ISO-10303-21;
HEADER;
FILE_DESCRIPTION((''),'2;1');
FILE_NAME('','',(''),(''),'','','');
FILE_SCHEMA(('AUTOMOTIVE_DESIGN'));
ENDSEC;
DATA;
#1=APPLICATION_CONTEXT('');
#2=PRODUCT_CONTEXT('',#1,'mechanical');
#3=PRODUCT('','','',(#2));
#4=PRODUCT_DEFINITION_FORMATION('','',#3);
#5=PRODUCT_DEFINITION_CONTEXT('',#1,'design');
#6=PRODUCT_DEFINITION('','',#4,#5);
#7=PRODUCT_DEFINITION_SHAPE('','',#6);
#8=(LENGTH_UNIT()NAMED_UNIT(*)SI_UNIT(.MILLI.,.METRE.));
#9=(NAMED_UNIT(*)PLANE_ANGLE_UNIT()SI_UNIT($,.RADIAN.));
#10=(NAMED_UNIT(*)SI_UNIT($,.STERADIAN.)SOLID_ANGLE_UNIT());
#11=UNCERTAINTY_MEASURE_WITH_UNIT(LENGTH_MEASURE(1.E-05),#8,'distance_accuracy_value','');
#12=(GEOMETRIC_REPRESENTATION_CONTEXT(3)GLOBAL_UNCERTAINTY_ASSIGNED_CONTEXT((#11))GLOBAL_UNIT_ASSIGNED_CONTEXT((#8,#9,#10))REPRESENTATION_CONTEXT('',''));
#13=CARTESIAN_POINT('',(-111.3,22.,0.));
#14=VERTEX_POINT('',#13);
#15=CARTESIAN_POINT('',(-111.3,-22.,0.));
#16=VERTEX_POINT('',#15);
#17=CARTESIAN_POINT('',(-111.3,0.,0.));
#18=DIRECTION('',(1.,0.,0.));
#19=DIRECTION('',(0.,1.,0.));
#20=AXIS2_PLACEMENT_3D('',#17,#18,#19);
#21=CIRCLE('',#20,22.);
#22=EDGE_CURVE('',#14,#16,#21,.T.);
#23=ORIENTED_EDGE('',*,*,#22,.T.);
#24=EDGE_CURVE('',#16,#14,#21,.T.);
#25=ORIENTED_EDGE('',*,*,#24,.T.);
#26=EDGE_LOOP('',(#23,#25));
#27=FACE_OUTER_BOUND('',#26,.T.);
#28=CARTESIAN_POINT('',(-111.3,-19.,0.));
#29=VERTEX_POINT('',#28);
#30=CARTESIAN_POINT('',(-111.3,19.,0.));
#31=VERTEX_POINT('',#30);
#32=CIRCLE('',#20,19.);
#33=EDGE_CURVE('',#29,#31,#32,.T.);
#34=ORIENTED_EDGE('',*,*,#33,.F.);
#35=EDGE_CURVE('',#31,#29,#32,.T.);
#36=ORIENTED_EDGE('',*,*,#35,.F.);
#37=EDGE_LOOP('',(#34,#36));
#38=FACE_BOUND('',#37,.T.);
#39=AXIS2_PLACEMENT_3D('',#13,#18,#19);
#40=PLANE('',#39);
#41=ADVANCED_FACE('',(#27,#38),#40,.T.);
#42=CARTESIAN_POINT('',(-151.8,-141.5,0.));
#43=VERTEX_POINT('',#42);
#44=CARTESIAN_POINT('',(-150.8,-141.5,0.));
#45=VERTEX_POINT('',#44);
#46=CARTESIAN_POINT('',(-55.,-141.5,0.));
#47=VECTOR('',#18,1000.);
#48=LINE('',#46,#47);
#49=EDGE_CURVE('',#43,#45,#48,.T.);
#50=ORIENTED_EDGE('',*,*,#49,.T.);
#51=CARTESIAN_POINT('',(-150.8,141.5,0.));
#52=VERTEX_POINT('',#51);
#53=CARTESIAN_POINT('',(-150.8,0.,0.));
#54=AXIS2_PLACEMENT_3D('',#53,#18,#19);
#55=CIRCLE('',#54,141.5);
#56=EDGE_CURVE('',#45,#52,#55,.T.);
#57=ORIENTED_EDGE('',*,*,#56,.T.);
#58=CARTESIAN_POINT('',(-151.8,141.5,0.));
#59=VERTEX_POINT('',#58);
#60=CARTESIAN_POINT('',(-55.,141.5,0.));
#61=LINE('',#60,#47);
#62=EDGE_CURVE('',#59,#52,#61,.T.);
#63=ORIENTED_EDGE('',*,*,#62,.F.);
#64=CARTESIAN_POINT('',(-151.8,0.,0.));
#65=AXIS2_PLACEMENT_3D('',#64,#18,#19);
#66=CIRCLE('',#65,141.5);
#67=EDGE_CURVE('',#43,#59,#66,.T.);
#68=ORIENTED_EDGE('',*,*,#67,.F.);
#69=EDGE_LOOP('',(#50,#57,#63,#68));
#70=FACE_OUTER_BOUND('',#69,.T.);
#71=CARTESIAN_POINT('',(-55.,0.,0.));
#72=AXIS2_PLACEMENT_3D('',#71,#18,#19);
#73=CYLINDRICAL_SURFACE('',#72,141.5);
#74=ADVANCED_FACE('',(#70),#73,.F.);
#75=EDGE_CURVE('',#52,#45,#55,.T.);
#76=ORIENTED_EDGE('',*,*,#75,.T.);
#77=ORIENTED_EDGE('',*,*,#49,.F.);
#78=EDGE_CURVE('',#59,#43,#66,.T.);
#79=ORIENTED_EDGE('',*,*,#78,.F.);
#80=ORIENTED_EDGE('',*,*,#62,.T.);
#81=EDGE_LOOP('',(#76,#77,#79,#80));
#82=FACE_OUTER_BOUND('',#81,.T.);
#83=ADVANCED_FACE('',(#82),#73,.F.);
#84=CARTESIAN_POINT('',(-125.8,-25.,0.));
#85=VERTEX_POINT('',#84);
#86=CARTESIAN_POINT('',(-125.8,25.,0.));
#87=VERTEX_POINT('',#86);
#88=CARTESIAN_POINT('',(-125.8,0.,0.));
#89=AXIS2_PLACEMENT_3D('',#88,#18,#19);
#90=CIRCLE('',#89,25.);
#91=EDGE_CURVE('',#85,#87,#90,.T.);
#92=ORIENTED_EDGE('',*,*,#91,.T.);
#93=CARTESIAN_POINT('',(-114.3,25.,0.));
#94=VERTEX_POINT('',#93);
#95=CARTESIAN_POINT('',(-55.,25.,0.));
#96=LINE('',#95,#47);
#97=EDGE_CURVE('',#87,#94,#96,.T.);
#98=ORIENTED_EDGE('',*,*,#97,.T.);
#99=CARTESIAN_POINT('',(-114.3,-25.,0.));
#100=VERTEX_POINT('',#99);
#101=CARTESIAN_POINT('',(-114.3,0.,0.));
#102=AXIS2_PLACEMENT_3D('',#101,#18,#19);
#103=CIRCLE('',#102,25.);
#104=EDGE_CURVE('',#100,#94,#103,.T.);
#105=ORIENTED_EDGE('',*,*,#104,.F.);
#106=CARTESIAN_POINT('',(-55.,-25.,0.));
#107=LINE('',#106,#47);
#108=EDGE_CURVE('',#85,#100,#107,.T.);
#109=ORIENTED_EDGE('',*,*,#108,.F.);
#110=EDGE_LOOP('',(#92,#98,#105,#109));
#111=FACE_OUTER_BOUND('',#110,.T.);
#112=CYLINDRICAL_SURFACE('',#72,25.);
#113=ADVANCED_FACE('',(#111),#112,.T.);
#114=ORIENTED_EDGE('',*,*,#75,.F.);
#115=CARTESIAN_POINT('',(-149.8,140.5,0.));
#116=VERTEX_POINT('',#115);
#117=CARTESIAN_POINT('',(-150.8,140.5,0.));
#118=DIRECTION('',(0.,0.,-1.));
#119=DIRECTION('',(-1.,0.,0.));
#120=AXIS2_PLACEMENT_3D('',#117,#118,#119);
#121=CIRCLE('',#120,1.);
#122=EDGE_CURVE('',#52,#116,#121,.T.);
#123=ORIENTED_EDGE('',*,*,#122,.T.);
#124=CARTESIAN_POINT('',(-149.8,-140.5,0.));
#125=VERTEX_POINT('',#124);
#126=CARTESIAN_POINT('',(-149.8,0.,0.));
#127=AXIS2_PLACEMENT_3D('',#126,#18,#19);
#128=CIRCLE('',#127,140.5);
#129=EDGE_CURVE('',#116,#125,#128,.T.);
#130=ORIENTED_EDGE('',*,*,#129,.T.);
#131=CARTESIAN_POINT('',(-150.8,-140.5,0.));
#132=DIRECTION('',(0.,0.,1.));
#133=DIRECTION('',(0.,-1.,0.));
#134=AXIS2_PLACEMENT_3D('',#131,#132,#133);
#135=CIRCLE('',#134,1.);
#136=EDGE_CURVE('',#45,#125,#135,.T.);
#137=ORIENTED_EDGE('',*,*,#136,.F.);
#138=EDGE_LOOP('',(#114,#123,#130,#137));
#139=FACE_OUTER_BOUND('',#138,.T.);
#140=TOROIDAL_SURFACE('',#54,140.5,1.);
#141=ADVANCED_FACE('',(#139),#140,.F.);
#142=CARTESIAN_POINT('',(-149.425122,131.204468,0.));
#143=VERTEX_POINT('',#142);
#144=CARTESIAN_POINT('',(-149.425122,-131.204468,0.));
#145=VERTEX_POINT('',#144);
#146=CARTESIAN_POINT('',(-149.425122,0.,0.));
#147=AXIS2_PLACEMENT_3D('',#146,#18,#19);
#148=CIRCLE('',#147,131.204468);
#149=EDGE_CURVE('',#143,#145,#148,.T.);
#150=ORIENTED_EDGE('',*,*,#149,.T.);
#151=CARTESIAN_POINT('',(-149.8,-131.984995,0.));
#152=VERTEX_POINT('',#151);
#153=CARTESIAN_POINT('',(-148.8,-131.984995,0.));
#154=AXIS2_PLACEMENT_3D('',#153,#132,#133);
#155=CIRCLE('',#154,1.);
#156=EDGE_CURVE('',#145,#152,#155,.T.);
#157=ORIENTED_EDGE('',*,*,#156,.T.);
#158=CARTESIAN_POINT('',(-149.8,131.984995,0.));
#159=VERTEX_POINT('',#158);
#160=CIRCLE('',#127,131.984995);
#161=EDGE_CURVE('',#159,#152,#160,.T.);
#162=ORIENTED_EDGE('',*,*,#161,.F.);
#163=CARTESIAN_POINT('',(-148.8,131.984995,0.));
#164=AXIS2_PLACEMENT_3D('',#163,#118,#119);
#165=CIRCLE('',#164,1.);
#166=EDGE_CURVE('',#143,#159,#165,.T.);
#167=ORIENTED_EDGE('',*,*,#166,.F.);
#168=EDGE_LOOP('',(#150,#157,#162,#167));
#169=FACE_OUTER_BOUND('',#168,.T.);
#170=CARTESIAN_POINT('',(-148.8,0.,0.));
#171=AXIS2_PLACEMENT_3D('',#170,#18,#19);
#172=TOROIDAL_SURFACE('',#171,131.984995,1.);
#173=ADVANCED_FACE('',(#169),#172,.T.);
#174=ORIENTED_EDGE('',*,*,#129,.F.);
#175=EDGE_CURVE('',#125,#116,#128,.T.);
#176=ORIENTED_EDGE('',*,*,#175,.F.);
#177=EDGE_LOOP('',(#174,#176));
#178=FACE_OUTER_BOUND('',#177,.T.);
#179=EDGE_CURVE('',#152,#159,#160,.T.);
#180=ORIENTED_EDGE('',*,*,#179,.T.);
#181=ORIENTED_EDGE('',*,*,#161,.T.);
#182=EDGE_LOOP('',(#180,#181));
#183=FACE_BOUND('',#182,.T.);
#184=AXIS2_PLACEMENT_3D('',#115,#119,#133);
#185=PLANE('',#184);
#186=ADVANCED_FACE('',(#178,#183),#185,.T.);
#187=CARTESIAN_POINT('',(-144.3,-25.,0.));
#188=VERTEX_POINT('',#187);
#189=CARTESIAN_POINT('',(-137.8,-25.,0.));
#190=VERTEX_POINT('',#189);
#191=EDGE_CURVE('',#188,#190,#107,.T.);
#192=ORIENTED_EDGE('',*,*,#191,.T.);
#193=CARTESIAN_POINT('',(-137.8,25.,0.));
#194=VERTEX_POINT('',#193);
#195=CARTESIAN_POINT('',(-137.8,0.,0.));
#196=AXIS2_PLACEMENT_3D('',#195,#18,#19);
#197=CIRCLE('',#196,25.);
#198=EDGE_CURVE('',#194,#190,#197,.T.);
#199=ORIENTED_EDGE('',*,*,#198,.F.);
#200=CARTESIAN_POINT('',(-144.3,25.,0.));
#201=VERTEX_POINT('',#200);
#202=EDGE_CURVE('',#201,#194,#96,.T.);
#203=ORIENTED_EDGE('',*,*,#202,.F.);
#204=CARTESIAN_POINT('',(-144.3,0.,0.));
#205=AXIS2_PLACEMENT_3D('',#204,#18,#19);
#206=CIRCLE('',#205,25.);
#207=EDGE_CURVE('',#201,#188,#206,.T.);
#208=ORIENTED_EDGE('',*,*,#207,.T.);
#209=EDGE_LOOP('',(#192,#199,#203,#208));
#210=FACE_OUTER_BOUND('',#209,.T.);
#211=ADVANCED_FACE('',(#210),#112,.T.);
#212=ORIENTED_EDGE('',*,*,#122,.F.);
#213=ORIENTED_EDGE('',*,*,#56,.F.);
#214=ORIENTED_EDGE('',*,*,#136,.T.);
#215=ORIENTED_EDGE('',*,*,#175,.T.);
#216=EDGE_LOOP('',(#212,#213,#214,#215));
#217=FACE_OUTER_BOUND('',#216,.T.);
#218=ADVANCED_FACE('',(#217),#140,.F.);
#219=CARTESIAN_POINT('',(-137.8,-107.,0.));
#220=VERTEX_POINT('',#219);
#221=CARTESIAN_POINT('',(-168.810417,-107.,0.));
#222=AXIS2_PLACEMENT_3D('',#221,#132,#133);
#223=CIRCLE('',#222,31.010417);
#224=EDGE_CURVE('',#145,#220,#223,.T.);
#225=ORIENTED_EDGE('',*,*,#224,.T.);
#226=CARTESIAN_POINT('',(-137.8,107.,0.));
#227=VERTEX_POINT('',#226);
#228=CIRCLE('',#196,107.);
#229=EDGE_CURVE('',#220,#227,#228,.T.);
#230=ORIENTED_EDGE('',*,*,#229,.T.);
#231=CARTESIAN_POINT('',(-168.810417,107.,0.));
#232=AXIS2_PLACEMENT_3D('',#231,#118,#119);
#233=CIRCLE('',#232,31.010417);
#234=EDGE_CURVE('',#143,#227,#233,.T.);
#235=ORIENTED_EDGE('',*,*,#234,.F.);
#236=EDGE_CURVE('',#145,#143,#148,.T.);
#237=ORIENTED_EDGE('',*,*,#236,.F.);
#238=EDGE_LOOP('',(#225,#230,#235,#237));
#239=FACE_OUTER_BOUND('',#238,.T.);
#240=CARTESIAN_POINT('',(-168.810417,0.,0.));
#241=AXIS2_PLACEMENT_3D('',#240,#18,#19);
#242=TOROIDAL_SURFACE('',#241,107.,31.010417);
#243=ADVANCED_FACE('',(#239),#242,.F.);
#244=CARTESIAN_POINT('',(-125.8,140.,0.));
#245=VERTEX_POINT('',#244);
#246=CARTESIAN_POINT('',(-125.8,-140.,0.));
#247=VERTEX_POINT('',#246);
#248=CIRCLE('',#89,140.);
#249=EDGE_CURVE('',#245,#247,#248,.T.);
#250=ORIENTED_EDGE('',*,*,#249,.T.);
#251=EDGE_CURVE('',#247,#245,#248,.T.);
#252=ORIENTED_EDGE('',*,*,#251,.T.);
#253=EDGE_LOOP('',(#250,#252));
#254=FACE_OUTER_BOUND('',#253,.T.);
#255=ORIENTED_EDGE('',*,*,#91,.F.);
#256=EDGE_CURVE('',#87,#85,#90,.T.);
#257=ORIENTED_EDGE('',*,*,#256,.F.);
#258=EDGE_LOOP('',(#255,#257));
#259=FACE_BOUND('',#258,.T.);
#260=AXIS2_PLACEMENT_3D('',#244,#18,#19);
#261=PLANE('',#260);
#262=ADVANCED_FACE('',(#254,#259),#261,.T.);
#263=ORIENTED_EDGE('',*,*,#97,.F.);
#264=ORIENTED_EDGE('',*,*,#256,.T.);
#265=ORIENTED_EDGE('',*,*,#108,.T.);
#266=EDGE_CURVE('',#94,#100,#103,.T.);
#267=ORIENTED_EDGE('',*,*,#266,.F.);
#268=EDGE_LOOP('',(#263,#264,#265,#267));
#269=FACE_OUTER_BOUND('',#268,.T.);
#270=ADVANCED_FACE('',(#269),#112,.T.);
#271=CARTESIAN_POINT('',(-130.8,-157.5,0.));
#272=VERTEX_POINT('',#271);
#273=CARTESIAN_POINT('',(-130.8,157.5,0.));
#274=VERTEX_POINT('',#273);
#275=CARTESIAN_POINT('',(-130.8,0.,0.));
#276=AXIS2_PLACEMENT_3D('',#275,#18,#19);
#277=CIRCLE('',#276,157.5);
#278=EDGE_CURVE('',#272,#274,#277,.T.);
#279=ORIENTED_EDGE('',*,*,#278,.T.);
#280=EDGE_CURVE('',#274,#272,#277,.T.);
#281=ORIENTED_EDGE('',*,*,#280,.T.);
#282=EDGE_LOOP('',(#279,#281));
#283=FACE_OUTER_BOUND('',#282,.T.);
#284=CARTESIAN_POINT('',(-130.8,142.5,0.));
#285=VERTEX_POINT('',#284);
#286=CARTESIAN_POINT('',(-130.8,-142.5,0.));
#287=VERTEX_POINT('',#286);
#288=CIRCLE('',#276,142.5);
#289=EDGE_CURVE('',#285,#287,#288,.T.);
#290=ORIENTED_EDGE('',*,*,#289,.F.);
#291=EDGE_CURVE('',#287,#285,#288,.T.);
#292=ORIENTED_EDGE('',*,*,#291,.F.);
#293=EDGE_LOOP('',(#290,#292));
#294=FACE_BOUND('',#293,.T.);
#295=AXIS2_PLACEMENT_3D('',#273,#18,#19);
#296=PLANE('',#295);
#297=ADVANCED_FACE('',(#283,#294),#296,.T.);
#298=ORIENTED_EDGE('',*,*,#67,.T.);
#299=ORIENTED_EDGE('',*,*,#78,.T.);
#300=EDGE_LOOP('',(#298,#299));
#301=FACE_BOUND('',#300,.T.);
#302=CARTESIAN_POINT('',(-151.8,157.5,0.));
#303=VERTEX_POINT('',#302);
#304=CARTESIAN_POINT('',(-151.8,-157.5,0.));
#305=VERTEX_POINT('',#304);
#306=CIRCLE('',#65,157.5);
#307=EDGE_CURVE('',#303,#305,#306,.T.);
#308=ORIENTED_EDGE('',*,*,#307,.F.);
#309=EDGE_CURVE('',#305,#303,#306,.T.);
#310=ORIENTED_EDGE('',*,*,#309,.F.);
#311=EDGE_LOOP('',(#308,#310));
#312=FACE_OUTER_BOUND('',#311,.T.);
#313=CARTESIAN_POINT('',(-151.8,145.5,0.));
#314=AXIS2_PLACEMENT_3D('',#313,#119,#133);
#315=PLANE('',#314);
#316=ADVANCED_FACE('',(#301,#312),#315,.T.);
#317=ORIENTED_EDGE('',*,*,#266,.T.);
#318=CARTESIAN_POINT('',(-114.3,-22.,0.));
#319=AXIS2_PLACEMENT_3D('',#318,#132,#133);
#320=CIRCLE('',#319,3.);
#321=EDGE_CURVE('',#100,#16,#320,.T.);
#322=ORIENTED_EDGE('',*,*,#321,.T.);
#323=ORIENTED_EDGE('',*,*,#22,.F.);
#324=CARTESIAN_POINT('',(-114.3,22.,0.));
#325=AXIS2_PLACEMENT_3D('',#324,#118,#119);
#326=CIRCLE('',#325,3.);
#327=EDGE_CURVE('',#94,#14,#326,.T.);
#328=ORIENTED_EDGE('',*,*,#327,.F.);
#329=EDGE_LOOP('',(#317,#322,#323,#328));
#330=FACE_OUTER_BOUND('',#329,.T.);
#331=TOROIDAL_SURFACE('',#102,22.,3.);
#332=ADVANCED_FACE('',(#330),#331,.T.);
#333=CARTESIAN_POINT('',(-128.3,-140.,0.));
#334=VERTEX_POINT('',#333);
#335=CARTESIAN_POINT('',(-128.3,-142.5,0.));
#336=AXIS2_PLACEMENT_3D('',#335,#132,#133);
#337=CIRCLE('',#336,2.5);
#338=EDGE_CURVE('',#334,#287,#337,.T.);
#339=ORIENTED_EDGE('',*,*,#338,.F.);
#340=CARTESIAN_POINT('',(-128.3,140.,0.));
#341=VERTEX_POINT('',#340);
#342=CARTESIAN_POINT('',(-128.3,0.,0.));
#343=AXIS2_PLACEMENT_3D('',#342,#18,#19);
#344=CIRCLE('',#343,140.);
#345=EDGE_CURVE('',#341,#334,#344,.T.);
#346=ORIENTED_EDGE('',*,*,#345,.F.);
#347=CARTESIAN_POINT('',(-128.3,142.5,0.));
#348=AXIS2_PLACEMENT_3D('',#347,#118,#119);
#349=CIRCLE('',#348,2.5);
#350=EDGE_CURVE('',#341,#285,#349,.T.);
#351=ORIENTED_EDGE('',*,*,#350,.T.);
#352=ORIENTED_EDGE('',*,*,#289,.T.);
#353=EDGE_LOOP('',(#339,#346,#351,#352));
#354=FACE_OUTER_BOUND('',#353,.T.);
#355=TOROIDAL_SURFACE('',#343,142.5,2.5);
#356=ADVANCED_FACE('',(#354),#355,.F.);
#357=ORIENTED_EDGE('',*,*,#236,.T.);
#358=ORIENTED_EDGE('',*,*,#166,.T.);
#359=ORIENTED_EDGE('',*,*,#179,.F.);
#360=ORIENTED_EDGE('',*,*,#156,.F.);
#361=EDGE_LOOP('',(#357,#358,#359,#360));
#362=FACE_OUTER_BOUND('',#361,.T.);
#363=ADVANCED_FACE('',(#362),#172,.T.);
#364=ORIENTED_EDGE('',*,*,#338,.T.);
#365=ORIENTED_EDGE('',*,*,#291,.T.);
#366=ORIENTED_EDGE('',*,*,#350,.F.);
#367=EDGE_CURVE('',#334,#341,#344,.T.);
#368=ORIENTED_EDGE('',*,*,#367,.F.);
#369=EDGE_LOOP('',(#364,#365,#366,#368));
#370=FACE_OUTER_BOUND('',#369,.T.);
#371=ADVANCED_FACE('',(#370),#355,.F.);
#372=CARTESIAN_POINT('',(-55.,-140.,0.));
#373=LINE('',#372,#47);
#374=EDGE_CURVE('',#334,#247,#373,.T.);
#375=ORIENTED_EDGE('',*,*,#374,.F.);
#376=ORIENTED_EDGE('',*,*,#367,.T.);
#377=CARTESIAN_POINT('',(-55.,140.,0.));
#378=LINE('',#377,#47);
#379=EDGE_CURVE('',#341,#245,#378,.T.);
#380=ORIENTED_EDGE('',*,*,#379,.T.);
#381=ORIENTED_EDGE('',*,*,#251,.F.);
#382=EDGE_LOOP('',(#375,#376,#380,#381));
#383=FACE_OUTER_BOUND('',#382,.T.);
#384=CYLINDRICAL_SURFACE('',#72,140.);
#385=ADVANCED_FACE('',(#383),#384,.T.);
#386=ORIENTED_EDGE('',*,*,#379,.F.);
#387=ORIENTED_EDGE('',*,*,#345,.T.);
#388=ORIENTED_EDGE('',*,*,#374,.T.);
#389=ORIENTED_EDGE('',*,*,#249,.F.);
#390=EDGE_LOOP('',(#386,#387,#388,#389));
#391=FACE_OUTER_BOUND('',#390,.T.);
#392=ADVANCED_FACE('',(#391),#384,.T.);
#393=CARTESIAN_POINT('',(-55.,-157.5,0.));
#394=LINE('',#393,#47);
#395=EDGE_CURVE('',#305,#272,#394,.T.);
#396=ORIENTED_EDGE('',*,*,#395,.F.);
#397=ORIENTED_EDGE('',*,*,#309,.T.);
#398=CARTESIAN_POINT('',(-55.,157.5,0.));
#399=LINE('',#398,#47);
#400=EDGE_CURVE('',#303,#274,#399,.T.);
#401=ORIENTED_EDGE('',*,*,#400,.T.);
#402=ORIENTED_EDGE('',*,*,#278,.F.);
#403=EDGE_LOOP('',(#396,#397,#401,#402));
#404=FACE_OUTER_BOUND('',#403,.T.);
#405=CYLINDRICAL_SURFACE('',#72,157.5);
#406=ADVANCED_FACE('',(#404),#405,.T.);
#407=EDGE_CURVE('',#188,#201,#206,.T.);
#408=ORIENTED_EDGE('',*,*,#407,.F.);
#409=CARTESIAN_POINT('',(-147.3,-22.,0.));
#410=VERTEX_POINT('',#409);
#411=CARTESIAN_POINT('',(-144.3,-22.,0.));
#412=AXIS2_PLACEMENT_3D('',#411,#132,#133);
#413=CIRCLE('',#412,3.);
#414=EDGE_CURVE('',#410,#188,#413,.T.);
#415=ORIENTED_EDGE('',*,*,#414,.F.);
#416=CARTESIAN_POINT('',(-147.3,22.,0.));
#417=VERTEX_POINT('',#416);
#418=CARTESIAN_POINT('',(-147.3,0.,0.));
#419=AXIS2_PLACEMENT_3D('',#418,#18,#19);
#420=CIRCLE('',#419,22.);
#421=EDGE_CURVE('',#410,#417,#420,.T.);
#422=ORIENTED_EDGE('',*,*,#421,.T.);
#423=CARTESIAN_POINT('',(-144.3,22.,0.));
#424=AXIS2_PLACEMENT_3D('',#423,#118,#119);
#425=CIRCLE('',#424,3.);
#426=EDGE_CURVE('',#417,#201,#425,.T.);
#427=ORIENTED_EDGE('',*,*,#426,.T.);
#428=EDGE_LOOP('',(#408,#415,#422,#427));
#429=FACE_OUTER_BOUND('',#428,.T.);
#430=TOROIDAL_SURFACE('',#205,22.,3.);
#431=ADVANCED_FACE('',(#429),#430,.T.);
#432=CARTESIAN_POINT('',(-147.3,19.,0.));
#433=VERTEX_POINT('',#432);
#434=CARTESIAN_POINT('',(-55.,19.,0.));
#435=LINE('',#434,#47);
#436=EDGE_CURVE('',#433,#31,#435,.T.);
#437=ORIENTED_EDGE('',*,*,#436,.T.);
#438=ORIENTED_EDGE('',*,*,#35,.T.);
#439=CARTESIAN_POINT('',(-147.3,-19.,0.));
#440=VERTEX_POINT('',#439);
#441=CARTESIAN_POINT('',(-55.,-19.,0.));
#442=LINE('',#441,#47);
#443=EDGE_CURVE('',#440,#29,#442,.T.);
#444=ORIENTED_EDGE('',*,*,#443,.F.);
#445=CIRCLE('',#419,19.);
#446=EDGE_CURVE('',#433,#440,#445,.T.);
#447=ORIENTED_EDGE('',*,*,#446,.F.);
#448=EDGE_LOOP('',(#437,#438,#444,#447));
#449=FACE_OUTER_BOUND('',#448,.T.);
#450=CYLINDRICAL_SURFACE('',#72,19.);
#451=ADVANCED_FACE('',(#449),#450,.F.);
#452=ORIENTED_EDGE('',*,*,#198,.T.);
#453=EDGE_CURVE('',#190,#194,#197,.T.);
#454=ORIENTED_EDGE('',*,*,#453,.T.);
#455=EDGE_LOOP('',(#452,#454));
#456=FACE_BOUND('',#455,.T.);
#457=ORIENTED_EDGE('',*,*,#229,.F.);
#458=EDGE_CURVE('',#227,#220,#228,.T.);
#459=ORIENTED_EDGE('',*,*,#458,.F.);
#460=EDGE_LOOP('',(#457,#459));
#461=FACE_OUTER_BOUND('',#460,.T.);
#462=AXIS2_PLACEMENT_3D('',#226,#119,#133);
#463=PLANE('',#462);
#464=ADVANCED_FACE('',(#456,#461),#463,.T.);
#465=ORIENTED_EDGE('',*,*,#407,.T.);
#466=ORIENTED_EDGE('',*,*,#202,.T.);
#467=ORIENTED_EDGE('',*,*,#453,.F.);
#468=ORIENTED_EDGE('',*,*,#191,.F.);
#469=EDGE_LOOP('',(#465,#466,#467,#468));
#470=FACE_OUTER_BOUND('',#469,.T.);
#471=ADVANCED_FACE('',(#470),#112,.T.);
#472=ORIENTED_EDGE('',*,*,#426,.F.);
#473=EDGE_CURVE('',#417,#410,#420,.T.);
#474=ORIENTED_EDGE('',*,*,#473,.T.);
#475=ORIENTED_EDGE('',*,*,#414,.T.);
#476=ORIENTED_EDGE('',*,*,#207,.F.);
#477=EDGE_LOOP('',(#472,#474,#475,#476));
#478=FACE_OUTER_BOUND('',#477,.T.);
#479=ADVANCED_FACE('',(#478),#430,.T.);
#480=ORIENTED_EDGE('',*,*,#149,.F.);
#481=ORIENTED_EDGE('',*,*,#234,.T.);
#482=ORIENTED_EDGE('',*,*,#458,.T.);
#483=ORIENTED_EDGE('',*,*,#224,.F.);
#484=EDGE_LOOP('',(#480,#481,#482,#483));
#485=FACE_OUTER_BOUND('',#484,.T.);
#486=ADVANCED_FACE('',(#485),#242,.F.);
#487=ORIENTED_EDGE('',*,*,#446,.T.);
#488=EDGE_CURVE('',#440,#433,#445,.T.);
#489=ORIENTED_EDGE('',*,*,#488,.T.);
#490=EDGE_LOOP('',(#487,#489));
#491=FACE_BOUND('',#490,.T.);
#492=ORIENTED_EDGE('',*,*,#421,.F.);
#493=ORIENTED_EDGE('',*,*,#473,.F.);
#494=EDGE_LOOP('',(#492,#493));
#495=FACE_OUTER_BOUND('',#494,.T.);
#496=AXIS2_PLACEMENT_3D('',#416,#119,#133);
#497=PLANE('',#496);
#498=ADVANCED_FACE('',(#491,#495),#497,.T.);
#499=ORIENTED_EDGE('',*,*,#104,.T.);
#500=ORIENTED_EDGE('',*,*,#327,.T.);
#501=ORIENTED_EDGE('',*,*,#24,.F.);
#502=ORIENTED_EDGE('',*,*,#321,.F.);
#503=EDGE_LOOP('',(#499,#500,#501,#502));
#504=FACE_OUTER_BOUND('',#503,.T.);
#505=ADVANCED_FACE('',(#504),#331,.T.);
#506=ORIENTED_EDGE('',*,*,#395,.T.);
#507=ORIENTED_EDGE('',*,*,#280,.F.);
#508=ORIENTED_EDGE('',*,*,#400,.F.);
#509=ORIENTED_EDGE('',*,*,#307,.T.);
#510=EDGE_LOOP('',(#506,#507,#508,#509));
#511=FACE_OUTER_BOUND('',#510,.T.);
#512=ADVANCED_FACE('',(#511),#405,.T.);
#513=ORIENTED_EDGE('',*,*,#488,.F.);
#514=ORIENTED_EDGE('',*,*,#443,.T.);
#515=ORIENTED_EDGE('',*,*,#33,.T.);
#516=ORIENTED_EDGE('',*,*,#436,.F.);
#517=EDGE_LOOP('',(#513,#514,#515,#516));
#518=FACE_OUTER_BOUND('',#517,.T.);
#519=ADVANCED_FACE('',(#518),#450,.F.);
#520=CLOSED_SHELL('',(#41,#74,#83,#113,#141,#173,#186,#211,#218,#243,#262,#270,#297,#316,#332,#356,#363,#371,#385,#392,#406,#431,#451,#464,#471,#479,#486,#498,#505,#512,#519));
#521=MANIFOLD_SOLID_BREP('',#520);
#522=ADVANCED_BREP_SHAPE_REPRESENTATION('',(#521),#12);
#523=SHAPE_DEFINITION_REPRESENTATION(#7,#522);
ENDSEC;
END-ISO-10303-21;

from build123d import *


with BuildPart() as part:
    # Sketch1 → Revolve1 (revolve)
    with BuildSketch(Plane.XY):
        with BuildLine():
            Line((-130.8, 157.5), (-151.8, 157.5))
            Line((-151.8, 157.5), (-151.8, 145.5))
            Line((-151.8, 145.5), (-151.8, 141.5))
            Line((-151.8, 141.5), (-150.8, 141.5))
            ThreePointArc((-150.8, 141.5), (-150.092893219, 141.207106781), (-149.8, 140.5))
            Line((-149.8, 140.5), (-149.8, 131.984995497))
            ThreePointArc((-149.8, 131.984995497), (-149.701421663, 131.552053256), (-149.425122031, 131.204468466))
            ThreePointArc((-149.425122031, 131.204468466), (-140.856955291, 120.42571931), (-137.8, 107))
            Line((-137.8, 107), (-137.8, 82.5))
            Line((-137.8, 82.5), (-137.8, 25))
            Line((-137.8, 25), (-144.3, 25))
            ThreePointArc((-144.3, 25), (-146.421320344, 24.121320344), (-147.3, 22))
            Line((-147.3, 22), (-147.3, 19))
            Line((-147.3, 19), (-111.3, 19))
            Line((-111.3, 19), (-111.3, 22))
            ThreePointArc((-111.3, 22), (-112.178679656, 24.121320344), (-114.3, 25))
            Line((-114.3, 25), (-125.8, 25))
            Line((-125.8, 25), (-125.8, 82.5))
            Line((-125.8, 82.5), (-125.8, 140))
            Line((-125.8, 140), (-128.3, 140))
            ThreePointArc((-128.3, 140), (-130.067766953, 140.732233047), (-130.8, 142.5))
            Line((-130.8, 142.5), (-130.8, 157.5))
        make_face()
    revolve(axis=Axis((-55, 0, 0), (-1, 0, 0)))


solid = part.part
